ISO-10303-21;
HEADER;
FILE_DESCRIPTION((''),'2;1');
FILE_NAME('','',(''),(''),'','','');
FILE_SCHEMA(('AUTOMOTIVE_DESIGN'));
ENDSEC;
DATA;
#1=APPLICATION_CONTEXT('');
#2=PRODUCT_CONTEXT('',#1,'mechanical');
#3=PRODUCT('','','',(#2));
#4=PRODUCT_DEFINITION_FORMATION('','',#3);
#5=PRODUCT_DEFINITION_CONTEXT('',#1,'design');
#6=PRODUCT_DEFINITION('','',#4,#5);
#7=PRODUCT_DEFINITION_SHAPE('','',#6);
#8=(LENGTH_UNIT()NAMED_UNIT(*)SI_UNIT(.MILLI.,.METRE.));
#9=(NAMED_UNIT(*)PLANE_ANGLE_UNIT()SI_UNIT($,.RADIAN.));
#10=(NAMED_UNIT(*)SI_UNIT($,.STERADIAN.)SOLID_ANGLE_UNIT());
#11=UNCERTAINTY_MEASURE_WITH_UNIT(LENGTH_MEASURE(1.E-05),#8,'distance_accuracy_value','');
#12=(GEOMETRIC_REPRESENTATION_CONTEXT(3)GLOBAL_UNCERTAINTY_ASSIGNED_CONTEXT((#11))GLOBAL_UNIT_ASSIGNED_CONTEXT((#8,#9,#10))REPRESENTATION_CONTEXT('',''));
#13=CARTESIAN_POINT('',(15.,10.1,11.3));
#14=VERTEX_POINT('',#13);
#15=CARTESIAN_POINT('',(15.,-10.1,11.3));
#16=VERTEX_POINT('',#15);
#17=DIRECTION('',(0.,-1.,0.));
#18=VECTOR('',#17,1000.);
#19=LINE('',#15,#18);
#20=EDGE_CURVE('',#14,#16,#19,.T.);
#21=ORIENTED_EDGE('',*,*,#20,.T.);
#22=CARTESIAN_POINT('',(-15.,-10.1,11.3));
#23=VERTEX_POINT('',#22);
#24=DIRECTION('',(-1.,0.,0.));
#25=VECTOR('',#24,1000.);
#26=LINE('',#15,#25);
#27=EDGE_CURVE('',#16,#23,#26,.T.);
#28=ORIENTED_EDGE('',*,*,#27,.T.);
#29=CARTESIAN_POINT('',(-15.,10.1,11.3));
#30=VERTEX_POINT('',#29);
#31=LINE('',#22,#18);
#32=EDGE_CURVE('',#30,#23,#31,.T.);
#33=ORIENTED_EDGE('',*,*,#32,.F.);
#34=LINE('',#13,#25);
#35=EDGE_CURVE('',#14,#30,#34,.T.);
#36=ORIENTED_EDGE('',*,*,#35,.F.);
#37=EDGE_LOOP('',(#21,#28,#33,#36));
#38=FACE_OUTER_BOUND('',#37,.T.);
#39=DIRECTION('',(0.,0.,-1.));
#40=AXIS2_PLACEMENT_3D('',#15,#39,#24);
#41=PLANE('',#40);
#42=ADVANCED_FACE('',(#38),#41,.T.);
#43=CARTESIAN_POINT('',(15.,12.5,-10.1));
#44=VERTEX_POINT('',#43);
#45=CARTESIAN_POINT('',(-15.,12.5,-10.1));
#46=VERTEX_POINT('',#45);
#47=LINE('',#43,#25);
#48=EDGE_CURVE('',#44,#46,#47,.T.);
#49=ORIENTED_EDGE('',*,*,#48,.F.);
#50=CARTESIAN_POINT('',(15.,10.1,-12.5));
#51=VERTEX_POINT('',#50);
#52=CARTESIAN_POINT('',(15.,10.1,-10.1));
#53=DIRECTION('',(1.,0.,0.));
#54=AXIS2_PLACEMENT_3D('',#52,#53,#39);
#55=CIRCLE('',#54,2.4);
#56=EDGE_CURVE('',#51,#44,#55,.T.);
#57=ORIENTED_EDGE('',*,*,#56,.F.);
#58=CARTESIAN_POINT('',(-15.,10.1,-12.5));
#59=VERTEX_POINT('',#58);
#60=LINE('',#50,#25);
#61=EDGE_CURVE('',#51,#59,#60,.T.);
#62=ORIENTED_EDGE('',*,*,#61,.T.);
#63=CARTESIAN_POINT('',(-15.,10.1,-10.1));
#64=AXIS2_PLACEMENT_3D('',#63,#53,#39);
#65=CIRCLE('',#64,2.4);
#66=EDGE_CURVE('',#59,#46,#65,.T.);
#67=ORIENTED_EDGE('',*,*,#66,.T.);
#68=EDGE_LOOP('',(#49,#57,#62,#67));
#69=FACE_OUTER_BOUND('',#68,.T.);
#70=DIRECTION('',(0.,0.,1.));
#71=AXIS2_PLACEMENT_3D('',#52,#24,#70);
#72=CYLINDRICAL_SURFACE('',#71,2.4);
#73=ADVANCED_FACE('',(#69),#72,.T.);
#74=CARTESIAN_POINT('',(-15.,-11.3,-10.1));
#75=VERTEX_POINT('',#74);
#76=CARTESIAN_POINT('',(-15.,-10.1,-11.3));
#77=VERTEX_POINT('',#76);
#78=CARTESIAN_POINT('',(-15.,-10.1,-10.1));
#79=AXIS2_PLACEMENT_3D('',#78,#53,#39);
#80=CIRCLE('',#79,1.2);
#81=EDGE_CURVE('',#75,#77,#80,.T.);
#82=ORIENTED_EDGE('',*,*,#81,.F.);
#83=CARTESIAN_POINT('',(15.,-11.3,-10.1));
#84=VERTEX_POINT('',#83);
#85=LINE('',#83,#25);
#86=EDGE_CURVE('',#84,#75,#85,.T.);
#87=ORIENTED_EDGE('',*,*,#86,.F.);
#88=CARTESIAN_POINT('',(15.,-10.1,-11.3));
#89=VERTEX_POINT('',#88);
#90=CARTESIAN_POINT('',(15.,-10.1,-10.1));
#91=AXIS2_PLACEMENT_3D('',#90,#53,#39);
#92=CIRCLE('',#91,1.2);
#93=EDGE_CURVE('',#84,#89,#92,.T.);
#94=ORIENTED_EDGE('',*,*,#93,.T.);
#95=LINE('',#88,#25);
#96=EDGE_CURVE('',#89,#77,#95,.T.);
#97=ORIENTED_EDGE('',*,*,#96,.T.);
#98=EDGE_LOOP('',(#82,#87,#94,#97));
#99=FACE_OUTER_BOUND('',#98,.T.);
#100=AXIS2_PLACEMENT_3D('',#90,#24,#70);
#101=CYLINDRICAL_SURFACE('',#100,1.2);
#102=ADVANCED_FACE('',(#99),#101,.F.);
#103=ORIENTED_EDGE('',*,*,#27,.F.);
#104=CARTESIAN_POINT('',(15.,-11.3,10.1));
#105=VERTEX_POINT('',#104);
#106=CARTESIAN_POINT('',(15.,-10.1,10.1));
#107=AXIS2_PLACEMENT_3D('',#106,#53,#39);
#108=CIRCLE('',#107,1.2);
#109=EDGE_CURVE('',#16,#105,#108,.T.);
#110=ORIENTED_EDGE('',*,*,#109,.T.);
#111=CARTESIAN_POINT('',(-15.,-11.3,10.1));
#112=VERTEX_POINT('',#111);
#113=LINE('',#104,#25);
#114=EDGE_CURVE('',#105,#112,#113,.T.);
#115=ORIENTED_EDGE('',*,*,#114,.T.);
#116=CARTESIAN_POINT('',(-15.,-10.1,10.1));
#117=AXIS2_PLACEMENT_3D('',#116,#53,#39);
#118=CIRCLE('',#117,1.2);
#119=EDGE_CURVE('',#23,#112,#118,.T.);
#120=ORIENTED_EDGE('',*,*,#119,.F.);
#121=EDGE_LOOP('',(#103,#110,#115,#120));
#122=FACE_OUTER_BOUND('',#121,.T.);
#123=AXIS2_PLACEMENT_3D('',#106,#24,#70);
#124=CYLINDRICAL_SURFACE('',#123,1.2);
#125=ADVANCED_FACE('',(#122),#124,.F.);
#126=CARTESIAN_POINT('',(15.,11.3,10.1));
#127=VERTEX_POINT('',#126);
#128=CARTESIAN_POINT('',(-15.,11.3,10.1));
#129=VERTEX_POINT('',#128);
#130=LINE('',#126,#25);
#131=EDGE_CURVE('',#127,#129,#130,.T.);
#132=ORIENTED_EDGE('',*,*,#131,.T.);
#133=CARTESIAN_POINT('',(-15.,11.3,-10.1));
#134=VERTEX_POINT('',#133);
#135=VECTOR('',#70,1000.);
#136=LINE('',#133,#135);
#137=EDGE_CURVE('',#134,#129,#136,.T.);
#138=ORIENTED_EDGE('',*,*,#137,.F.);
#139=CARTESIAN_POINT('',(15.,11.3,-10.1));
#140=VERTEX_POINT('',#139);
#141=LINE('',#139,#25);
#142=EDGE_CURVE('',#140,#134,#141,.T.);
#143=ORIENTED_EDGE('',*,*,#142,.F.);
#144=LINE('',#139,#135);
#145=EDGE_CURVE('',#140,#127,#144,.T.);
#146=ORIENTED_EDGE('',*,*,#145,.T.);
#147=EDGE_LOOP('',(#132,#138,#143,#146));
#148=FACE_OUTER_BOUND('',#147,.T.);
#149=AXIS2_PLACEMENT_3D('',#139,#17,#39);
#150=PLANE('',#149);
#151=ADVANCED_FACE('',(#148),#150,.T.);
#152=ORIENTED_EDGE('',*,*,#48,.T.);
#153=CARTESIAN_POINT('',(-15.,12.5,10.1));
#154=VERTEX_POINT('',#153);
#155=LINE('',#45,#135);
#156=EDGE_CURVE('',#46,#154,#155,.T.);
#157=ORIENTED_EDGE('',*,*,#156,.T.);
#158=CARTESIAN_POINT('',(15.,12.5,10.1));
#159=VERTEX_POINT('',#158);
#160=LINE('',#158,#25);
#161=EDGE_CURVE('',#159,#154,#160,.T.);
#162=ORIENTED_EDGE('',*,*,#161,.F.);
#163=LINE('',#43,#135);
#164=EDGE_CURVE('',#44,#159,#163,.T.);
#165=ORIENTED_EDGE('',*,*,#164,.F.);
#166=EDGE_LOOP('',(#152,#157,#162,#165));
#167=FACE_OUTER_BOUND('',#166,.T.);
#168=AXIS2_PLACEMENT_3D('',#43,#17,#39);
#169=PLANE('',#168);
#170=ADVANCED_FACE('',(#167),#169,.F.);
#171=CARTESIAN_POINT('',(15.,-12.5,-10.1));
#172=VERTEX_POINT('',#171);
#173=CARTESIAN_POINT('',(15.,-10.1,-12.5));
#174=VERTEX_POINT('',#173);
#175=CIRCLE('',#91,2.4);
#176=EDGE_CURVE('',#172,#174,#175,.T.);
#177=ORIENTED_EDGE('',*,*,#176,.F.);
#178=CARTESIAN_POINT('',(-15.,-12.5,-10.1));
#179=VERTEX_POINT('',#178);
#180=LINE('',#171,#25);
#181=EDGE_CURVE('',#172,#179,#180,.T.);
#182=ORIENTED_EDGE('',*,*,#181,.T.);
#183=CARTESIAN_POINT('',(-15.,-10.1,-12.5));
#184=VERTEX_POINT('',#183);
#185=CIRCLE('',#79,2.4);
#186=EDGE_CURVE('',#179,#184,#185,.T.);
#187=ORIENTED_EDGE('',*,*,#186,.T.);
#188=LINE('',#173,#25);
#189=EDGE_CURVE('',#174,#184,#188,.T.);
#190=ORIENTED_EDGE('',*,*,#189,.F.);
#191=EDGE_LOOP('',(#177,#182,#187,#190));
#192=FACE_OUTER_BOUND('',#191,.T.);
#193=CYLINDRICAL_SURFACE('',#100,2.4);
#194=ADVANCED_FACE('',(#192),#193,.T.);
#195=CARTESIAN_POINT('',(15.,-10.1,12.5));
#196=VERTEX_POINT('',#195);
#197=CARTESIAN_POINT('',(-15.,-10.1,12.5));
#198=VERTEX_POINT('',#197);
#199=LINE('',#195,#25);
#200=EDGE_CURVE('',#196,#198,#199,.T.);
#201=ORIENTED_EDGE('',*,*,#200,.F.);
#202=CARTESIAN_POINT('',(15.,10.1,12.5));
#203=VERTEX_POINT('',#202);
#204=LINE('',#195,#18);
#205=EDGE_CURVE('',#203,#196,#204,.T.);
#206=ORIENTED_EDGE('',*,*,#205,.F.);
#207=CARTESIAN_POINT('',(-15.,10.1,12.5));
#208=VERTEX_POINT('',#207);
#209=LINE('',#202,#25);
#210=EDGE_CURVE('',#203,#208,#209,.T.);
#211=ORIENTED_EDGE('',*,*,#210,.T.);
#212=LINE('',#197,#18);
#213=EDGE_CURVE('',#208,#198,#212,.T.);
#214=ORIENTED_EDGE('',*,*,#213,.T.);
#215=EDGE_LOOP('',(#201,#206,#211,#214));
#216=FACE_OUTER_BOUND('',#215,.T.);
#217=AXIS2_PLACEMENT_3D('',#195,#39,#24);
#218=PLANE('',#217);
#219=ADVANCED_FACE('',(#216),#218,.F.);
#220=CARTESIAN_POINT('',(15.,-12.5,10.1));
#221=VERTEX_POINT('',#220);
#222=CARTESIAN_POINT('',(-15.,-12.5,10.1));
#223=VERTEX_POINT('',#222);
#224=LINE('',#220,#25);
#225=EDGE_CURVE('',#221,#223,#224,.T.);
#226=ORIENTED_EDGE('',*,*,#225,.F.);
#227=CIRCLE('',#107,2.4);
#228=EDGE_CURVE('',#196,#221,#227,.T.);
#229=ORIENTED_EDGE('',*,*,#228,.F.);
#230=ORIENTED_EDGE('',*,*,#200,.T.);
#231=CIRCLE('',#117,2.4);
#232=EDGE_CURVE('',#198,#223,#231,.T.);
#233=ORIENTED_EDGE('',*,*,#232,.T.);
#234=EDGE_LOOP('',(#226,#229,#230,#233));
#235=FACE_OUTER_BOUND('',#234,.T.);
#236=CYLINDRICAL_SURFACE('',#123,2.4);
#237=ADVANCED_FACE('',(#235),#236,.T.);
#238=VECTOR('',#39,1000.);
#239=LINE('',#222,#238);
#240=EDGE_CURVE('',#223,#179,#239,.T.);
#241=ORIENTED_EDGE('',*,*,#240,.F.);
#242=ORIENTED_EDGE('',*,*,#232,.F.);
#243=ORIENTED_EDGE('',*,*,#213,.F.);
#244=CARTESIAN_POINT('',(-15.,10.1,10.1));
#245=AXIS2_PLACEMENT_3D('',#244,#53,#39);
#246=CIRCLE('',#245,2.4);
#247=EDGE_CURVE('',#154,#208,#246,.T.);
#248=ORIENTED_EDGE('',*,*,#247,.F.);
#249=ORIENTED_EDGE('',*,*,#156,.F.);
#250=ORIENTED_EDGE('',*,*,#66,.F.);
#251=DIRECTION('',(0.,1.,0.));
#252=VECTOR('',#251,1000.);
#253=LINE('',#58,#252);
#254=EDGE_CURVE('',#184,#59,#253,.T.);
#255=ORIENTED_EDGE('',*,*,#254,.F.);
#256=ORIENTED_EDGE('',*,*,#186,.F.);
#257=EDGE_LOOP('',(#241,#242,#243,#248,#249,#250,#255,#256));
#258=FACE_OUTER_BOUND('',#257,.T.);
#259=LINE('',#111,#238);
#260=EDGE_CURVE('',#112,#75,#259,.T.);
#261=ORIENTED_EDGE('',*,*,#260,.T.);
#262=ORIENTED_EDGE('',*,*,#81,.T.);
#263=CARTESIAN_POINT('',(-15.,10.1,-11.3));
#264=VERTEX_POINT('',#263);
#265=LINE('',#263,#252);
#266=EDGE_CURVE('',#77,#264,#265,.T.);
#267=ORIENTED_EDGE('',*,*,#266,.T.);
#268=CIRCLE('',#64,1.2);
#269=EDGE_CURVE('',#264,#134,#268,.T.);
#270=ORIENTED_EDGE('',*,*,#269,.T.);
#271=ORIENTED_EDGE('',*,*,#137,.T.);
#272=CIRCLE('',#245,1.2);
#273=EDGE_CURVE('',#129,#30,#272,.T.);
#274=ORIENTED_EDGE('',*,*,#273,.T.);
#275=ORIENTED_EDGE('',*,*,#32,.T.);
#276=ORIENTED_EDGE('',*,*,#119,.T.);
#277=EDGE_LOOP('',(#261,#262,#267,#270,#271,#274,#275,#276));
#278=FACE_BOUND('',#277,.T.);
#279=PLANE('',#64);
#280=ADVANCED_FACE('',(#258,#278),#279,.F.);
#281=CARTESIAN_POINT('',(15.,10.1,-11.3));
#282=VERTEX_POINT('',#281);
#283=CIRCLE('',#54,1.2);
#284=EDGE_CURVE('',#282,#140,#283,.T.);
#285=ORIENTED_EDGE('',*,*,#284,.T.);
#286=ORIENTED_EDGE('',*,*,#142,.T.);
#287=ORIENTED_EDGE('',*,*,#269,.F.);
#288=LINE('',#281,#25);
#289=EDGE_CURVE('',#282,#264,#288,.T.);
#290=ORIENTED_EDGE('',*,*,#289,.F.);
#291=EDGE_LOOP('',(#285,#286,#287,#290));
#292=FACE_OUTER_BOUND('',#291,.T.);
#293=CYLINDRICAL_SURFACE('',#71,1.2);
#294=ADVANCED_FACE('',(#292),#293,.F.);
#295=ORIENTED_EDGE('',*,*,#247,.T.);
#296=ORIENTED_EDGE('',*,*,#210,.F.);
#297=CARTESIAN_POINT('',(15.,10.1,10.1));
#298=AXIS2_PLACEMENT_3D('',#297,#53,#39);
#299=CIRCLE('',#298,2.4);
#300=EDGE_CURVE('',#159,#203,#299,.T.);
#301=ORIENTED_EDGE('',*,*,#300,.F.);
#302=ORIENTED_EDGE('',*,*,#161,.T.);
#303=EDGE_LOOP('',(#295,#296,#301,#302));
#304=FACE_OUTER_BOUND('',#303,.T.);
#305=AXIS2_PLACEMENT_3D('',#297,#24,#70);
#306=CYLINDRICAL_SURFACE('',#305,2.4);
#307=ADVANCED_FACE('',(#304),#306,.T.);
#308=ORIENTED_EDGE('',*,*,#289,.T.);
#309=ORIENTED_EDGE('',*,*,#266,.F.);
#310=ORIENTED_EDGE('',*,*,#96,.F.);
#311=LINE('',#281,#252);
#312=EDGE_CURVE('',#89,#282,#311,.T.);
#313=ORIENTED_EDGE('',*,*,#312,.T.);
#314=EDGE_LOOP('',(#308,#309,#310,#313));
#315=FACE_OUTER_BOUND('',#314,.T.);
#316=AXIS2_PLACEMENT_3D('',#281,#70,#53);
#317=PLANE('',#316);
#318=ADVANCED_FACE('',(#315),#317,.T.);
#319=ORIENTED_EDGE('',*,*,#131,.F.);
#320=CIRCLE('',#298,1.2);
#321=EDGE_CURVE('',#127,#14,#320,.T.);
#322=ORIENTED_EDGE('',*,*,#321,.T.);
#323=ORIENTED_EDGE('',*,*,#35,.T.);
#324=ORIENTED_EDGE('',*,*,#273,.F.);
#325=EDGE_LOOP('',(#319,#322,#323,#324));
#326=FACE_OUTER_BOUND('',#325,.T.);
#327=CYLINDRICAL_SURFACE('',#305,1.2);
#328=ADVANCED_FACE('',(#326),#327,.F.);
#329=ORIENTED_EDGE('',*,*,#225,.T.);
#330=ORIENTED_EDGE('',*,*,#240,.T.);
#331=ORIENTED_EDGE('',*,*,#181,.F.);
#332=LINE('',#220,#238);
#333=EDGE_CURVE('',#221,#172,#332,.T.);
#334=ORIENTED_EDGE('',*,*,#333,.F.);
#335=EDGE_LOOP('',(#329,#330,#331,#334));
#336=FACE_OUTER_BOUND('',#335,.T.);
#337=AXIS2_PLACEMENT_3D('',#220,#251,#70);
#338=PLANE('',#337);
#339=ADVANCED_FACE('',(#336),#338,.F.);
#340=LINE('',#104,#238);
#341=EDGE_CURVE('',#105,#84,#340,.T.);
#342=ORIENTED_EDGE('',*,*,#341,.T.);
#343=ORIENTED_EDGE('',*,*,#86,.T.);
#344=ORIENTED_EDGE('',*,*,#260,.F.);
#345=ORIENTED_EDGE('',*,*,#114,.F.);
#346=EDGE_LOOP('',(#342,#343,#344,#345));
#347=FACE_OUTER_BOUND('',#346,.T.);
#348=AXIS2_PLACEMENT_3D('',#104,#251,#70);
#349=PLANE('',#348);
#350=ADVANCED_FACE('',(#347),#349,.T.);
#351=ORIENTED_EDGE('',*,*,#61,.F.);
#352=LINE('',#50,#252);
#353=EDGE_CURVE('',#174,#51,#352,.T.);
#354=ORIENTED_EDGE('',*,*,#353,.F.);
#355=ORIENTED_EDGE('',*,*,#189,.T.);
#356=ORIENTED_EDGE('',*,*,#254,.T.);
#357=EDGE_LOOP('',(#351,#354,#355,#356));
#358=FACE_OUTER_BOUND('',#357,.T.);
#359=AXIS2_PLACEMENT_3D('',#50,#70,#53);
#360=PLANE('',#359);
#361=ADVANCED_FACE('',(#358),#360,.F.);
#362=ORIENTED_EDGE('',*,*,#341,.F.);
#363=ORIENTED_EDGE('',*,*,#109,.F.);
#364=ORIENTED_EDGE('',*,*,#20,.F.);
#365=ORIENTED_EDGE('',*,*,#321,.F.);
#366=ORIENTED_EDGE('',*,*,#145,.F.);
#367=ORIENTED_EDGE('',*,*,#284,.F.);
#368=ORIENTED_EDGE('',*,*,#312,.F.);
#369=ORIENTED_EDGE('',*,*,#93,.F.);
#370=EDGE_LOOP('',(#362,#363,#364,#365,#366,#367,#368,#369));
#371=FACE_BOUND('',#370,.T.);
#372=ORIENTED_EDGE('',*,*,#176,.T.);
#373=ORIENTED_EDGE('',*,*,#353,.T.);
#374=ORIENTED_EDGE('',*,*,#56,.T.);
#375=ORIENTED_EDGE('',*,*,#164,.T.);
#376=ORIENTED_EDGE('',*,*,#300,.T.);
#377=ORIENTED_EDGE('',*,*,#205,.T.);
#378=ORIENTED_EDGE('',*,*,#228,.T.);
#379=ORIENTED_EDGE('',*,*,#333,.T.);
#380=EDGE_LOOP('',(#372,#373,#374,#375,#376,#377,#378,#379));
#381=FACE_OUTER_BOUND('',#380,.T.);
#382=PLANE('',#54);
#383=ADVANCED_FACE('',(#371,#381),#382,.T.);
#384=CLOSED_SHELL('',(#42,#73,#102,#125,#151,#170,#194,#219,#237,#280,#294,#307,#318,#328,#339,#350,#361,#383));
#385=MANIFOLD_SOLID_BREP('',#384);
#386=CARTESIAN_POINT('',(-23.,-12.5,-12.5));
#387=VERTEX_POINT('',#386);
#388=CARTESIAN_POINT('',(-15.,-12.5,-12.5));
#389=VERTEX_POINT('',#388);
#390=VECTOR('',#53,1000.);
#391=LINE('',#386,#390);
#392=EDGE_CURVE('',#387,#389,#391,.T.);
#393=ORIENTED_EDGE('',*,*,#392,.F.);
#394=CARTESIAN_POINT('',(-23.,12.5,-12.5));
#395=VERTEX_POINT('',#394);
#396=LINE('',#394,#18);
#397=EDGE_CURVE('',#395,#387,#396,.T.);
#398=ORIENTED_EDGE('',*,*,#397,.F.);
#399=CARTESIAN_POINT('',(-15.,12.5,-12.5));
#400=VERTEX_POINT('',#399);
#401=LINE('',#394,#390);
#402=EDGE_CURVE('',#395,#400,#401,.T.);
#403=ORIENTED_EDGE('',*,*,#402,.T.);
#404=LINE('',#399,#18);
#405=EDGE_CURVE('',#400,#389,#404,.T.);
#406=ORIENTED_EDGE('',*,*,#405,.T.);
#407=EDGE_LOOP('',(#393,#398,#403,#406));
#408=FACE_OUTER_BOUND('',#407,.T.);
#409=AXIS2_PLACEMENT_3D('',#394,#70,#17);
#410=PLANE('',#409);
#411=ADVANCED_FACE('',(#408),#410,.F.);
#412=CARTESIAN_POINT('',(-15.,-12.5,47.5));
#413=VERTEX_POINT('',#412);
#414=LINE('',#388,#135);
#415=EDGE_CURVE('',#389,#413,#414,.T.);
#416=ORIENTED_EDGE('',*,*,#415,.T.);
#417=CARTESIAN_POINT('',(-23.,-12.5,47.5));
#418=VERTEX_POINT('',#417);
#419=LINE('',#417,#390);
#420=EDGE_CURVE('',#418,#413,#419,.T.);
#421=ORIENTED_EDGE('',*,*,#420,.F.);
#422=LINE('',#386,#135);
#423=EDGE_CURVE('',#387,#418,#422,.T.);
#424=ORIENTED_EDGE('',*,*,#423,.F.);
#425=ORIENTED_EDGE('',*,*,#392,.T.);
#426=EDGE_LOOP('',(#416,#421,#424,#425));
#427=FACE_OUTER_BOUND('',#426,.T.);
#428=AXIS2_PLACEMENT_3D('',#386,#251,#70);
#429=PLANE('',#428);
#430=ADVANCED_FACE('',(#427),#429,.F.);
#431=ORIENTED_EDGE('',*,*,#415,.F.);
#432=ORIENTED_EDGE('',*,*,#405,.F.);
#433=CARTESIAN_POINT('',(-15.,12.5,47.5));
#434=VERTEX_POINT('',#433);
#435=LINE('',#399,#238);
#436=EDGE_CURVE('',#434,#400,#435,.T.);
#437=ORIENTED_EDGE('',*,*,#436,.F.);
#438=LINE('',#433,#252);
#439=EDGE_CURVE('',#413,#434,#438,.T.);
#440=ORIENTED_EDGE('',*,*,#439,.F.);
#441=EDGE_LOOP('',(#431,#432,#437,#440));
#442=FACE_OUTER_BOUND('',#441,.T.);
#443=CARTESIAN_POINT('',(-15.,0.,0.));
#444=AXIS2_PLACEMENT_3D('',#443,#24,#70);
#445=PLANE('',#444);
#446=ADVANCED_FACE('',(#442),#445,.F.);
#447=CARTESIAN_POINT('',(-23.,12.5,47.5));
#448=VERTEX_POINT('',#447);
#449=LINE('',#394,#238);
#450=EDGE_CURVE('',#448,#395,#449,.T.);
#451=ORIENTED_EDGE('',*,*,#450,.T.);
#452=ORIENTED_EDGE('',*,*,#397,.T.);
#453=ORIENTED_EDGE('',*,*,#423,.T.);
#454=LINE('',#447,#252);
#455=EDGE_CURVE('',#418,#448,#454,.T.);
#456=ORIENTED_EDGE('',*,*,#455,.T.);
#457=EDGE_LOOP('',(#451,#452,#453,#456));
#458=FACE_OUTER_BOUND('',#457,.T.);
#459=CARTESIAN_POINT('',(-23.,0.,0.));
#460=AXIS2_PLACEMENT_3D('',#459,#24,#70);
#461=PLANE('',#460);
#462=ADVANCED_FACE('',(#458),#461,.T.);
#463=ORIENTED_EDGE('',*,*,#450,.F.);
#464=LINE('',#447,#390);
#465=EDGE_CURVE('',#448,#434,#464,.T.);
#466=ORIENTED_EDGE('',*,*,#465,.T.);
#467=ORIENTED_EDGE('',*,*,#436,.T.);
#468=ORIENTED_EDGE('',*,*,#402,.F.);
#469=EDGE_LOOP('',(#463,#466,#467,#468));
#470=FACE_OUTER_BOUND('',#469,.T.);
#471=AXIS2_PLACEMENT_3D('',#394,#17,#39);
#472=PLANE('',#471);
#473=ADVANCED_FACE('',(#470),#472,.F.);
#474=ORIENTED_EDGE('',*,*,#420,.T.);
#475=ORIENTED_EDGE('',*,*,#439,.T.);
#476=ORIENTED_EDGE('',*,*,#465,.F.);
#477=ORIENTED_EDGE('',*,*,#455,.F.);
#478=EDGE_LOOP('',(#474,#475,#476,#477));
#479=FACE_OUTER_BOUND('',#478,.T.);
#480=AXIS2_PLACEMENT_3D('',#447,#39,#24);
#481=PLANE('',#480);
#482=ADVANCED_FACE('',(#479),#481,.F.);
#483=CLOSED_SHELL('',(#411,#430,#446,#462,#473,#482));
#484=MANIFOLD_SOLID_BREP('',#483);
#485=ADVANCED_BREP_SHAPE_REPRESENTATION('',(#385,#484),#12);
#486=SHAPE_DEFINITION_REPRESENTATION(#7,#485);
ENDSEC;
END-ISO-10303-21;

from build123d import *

# Parameters (mm, degrees)
GB_6728_1986_SQUARE_HOLLOW_SECTION_025_X_DEPTH = 30
SKETCH3_W                                      = 60
SKETCH3_H                                      = 25
BOSS_EXTRUDE1_DEPTH                            = 8


with BuildPart() as part:
    # Sketch1 → Gb／6728-1986 square hollow section 025 X 25 X 1.2(1) (new body)
    with BuildSketch(Plane(origin=(-15, 0, 0), x_dir=(0, 0, -1), z_dir=(1, 0, 0))):
        with BuildLine():
            Line((-10.1, -12.5), (10.1, -12.5))
            ThreePointArc((10.1, -12.5), (11.797056275, -11.797056275), (12.5, -10.1))
            Line((12.5, -10.1), (12.5, 10.1))
            ThreePointArc((12.5, 10.1), (11.797056275, 11.797056275), (10.1, 12.5))
            Line((10.1, 12.5), (-10.1, 12.5))
            ThreePointArc((-10.1, 12.5), (-11.797056275, 11.797056275), (-12.5, 10.1))
            Line((-12.5, 10.1), (-12.5, -10.1))
            ThreePointArc((-12.5, -10.1), (-11.797056275, -11.797056275), (-10.1, -12.5))
        make_face()
        with BuildLine():
            Line((-10.1, -11.3), (10.1, -11.3))
            ThreePointArc((10.1, -11.3), (10.948528137, -10.948528137), (11.3, -10.1))
            Line((11.3, -10.1), (11.3, 10.1))
            ThreePointArc((11.3, 10.1), (10.948528137, 10.948528137), (10.1, 11.3))
            Line((10.1, 11.3), (-10.1, 11.3))
            ThreePointArc((-10.1, 11.3), (-10.948528137, 10.948528137), (-11.3, 10.1))
            Line((-11.3, 10.1), (-11.3, -10.1))
            ThreePointArc((-11.3, -10.1), (-10.948528137, -10.948528137), (-10.1, -11.3))
        make_face(mode=Mode.SUBTRACT)
    extrude(amount=GB_6728_1986_SQUARE_HOLLOW_SECTION_025_X_DEPTH)


with BuildPart() as body_2:
    # Sketch3 → Boss-Extrude1 (new body)
    with BuildSketch(Plane.ZY.offset(15)):
        with Locations((17.5, 0)):
            Rectangle(SKETCH3_W, SKETCH3_H)
    extrude(amount=BOSS_EXTRUDE1_DEPTH)


solid = Compound([part.part, body_2.part])
